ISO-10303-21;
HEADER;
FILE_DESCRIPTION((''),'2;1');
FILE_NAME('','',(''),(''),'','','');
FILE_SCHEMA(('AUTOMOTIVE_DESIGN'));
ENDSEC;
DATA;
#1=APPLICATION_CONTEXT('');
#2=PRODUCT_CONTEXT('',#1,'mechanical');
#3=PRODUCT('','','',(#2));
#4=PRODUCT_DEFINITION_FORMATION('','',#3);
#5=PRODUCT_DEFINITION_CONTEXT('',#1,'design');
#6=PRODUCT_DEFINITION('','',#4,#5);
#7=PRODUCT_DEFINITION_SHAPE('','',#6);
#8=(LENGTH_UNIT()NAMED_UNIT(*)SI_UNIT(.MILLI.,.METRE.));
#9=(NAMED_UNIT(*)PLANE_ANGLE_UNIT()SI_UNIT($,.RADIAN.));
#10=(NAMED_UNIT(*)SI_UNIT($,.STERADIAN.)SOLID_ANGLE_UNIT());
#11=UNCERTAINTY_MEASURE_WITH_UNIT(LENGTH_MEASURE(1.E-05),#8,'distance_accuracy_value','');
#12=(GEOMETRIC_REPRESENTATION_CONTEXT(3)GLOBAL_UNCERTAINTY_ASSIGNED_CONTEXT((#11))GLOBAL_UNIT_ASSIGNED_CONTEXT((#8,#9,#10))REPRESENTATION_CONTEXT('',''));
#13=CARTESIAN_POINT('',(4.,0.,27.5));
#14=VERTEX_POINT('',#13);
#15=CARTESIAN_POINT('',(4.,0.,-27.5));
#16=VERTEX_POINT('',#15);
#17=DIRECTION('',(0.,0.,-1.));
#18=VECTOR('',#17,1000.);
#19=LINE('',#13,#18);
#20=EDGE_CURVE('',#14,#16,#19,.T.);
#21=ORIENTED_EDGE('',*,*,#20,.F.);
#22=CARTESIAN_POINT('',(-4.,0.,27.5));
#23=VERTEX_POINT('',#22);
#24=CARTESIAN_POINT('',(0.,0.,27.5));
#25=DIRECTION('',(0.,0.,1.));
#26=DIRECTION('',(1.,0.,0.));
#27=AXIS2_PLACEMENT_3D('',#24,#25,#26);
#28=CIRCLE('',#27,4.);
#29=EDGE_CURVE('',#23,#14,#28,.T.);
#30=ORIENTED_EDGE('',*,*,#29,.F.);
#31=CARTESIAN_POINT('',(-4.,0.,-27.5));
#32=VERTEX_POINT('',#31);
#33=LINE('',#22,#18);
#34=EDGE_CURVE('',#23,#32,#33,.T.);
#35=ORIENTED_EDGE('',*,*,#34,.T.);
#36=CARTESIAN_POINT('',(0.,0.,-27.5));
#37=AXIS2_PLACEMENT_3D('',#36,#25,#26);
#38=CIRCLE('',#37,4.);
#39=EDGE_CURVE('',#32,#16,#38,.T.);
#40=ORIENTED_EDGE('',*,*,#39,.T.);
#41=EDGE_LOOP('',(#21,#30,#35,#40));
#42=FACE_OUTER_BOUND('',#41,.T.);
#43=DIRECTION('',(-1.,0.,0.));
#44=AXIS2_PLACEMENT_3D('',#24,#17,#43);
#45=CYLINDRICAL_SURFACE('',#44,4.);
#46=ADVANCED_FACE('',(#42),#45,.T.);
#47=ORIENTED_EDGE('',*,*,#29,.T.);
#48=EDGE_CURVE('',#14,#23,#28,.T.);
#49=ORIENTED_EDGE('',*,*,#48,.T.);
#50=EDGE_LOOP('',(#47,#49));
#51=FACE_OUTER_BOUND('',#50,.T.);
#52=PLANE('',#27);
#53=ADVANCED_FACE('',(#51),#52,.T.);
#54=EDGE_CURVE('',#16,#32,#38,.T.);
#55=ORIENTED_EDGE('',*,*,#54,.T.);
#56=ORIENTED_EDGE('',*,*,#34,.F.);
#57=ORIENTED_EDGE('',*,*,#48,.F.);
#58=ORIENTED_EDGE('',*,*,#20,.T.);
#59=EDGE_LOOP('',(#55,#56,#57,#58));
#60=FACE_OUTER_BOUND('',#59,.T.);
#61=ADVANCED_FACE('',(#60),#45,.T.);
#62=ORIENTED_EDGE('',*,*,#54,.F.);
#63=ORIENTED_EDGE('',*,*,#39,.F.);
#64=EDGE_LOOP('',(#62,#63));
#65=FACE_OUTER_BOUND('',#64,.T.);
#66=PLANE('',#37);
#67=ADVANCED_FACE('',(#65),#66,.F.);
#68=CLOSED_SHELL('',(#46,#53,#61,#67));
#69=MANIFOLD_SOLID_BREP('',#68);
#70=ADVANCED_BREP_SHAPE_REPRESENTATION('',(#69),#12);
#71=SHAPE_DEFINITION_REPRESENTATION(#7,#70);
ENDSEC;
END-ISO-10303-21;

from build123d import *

# Parameters (mm, degrees)
SKETCH_1_R      = 4
EXTRUDE_1_DEPTH = 27.5


with BuildPart() as part:
    # 草图1 → 凸台-拉伸1 (new, symmetric)
    with BuildSketch(Plane.XY):
        Circle(SKETCH_1_R)
    extrude(amount=EXTRUDE_1_DEPTH, both=True)


solid = part.part
